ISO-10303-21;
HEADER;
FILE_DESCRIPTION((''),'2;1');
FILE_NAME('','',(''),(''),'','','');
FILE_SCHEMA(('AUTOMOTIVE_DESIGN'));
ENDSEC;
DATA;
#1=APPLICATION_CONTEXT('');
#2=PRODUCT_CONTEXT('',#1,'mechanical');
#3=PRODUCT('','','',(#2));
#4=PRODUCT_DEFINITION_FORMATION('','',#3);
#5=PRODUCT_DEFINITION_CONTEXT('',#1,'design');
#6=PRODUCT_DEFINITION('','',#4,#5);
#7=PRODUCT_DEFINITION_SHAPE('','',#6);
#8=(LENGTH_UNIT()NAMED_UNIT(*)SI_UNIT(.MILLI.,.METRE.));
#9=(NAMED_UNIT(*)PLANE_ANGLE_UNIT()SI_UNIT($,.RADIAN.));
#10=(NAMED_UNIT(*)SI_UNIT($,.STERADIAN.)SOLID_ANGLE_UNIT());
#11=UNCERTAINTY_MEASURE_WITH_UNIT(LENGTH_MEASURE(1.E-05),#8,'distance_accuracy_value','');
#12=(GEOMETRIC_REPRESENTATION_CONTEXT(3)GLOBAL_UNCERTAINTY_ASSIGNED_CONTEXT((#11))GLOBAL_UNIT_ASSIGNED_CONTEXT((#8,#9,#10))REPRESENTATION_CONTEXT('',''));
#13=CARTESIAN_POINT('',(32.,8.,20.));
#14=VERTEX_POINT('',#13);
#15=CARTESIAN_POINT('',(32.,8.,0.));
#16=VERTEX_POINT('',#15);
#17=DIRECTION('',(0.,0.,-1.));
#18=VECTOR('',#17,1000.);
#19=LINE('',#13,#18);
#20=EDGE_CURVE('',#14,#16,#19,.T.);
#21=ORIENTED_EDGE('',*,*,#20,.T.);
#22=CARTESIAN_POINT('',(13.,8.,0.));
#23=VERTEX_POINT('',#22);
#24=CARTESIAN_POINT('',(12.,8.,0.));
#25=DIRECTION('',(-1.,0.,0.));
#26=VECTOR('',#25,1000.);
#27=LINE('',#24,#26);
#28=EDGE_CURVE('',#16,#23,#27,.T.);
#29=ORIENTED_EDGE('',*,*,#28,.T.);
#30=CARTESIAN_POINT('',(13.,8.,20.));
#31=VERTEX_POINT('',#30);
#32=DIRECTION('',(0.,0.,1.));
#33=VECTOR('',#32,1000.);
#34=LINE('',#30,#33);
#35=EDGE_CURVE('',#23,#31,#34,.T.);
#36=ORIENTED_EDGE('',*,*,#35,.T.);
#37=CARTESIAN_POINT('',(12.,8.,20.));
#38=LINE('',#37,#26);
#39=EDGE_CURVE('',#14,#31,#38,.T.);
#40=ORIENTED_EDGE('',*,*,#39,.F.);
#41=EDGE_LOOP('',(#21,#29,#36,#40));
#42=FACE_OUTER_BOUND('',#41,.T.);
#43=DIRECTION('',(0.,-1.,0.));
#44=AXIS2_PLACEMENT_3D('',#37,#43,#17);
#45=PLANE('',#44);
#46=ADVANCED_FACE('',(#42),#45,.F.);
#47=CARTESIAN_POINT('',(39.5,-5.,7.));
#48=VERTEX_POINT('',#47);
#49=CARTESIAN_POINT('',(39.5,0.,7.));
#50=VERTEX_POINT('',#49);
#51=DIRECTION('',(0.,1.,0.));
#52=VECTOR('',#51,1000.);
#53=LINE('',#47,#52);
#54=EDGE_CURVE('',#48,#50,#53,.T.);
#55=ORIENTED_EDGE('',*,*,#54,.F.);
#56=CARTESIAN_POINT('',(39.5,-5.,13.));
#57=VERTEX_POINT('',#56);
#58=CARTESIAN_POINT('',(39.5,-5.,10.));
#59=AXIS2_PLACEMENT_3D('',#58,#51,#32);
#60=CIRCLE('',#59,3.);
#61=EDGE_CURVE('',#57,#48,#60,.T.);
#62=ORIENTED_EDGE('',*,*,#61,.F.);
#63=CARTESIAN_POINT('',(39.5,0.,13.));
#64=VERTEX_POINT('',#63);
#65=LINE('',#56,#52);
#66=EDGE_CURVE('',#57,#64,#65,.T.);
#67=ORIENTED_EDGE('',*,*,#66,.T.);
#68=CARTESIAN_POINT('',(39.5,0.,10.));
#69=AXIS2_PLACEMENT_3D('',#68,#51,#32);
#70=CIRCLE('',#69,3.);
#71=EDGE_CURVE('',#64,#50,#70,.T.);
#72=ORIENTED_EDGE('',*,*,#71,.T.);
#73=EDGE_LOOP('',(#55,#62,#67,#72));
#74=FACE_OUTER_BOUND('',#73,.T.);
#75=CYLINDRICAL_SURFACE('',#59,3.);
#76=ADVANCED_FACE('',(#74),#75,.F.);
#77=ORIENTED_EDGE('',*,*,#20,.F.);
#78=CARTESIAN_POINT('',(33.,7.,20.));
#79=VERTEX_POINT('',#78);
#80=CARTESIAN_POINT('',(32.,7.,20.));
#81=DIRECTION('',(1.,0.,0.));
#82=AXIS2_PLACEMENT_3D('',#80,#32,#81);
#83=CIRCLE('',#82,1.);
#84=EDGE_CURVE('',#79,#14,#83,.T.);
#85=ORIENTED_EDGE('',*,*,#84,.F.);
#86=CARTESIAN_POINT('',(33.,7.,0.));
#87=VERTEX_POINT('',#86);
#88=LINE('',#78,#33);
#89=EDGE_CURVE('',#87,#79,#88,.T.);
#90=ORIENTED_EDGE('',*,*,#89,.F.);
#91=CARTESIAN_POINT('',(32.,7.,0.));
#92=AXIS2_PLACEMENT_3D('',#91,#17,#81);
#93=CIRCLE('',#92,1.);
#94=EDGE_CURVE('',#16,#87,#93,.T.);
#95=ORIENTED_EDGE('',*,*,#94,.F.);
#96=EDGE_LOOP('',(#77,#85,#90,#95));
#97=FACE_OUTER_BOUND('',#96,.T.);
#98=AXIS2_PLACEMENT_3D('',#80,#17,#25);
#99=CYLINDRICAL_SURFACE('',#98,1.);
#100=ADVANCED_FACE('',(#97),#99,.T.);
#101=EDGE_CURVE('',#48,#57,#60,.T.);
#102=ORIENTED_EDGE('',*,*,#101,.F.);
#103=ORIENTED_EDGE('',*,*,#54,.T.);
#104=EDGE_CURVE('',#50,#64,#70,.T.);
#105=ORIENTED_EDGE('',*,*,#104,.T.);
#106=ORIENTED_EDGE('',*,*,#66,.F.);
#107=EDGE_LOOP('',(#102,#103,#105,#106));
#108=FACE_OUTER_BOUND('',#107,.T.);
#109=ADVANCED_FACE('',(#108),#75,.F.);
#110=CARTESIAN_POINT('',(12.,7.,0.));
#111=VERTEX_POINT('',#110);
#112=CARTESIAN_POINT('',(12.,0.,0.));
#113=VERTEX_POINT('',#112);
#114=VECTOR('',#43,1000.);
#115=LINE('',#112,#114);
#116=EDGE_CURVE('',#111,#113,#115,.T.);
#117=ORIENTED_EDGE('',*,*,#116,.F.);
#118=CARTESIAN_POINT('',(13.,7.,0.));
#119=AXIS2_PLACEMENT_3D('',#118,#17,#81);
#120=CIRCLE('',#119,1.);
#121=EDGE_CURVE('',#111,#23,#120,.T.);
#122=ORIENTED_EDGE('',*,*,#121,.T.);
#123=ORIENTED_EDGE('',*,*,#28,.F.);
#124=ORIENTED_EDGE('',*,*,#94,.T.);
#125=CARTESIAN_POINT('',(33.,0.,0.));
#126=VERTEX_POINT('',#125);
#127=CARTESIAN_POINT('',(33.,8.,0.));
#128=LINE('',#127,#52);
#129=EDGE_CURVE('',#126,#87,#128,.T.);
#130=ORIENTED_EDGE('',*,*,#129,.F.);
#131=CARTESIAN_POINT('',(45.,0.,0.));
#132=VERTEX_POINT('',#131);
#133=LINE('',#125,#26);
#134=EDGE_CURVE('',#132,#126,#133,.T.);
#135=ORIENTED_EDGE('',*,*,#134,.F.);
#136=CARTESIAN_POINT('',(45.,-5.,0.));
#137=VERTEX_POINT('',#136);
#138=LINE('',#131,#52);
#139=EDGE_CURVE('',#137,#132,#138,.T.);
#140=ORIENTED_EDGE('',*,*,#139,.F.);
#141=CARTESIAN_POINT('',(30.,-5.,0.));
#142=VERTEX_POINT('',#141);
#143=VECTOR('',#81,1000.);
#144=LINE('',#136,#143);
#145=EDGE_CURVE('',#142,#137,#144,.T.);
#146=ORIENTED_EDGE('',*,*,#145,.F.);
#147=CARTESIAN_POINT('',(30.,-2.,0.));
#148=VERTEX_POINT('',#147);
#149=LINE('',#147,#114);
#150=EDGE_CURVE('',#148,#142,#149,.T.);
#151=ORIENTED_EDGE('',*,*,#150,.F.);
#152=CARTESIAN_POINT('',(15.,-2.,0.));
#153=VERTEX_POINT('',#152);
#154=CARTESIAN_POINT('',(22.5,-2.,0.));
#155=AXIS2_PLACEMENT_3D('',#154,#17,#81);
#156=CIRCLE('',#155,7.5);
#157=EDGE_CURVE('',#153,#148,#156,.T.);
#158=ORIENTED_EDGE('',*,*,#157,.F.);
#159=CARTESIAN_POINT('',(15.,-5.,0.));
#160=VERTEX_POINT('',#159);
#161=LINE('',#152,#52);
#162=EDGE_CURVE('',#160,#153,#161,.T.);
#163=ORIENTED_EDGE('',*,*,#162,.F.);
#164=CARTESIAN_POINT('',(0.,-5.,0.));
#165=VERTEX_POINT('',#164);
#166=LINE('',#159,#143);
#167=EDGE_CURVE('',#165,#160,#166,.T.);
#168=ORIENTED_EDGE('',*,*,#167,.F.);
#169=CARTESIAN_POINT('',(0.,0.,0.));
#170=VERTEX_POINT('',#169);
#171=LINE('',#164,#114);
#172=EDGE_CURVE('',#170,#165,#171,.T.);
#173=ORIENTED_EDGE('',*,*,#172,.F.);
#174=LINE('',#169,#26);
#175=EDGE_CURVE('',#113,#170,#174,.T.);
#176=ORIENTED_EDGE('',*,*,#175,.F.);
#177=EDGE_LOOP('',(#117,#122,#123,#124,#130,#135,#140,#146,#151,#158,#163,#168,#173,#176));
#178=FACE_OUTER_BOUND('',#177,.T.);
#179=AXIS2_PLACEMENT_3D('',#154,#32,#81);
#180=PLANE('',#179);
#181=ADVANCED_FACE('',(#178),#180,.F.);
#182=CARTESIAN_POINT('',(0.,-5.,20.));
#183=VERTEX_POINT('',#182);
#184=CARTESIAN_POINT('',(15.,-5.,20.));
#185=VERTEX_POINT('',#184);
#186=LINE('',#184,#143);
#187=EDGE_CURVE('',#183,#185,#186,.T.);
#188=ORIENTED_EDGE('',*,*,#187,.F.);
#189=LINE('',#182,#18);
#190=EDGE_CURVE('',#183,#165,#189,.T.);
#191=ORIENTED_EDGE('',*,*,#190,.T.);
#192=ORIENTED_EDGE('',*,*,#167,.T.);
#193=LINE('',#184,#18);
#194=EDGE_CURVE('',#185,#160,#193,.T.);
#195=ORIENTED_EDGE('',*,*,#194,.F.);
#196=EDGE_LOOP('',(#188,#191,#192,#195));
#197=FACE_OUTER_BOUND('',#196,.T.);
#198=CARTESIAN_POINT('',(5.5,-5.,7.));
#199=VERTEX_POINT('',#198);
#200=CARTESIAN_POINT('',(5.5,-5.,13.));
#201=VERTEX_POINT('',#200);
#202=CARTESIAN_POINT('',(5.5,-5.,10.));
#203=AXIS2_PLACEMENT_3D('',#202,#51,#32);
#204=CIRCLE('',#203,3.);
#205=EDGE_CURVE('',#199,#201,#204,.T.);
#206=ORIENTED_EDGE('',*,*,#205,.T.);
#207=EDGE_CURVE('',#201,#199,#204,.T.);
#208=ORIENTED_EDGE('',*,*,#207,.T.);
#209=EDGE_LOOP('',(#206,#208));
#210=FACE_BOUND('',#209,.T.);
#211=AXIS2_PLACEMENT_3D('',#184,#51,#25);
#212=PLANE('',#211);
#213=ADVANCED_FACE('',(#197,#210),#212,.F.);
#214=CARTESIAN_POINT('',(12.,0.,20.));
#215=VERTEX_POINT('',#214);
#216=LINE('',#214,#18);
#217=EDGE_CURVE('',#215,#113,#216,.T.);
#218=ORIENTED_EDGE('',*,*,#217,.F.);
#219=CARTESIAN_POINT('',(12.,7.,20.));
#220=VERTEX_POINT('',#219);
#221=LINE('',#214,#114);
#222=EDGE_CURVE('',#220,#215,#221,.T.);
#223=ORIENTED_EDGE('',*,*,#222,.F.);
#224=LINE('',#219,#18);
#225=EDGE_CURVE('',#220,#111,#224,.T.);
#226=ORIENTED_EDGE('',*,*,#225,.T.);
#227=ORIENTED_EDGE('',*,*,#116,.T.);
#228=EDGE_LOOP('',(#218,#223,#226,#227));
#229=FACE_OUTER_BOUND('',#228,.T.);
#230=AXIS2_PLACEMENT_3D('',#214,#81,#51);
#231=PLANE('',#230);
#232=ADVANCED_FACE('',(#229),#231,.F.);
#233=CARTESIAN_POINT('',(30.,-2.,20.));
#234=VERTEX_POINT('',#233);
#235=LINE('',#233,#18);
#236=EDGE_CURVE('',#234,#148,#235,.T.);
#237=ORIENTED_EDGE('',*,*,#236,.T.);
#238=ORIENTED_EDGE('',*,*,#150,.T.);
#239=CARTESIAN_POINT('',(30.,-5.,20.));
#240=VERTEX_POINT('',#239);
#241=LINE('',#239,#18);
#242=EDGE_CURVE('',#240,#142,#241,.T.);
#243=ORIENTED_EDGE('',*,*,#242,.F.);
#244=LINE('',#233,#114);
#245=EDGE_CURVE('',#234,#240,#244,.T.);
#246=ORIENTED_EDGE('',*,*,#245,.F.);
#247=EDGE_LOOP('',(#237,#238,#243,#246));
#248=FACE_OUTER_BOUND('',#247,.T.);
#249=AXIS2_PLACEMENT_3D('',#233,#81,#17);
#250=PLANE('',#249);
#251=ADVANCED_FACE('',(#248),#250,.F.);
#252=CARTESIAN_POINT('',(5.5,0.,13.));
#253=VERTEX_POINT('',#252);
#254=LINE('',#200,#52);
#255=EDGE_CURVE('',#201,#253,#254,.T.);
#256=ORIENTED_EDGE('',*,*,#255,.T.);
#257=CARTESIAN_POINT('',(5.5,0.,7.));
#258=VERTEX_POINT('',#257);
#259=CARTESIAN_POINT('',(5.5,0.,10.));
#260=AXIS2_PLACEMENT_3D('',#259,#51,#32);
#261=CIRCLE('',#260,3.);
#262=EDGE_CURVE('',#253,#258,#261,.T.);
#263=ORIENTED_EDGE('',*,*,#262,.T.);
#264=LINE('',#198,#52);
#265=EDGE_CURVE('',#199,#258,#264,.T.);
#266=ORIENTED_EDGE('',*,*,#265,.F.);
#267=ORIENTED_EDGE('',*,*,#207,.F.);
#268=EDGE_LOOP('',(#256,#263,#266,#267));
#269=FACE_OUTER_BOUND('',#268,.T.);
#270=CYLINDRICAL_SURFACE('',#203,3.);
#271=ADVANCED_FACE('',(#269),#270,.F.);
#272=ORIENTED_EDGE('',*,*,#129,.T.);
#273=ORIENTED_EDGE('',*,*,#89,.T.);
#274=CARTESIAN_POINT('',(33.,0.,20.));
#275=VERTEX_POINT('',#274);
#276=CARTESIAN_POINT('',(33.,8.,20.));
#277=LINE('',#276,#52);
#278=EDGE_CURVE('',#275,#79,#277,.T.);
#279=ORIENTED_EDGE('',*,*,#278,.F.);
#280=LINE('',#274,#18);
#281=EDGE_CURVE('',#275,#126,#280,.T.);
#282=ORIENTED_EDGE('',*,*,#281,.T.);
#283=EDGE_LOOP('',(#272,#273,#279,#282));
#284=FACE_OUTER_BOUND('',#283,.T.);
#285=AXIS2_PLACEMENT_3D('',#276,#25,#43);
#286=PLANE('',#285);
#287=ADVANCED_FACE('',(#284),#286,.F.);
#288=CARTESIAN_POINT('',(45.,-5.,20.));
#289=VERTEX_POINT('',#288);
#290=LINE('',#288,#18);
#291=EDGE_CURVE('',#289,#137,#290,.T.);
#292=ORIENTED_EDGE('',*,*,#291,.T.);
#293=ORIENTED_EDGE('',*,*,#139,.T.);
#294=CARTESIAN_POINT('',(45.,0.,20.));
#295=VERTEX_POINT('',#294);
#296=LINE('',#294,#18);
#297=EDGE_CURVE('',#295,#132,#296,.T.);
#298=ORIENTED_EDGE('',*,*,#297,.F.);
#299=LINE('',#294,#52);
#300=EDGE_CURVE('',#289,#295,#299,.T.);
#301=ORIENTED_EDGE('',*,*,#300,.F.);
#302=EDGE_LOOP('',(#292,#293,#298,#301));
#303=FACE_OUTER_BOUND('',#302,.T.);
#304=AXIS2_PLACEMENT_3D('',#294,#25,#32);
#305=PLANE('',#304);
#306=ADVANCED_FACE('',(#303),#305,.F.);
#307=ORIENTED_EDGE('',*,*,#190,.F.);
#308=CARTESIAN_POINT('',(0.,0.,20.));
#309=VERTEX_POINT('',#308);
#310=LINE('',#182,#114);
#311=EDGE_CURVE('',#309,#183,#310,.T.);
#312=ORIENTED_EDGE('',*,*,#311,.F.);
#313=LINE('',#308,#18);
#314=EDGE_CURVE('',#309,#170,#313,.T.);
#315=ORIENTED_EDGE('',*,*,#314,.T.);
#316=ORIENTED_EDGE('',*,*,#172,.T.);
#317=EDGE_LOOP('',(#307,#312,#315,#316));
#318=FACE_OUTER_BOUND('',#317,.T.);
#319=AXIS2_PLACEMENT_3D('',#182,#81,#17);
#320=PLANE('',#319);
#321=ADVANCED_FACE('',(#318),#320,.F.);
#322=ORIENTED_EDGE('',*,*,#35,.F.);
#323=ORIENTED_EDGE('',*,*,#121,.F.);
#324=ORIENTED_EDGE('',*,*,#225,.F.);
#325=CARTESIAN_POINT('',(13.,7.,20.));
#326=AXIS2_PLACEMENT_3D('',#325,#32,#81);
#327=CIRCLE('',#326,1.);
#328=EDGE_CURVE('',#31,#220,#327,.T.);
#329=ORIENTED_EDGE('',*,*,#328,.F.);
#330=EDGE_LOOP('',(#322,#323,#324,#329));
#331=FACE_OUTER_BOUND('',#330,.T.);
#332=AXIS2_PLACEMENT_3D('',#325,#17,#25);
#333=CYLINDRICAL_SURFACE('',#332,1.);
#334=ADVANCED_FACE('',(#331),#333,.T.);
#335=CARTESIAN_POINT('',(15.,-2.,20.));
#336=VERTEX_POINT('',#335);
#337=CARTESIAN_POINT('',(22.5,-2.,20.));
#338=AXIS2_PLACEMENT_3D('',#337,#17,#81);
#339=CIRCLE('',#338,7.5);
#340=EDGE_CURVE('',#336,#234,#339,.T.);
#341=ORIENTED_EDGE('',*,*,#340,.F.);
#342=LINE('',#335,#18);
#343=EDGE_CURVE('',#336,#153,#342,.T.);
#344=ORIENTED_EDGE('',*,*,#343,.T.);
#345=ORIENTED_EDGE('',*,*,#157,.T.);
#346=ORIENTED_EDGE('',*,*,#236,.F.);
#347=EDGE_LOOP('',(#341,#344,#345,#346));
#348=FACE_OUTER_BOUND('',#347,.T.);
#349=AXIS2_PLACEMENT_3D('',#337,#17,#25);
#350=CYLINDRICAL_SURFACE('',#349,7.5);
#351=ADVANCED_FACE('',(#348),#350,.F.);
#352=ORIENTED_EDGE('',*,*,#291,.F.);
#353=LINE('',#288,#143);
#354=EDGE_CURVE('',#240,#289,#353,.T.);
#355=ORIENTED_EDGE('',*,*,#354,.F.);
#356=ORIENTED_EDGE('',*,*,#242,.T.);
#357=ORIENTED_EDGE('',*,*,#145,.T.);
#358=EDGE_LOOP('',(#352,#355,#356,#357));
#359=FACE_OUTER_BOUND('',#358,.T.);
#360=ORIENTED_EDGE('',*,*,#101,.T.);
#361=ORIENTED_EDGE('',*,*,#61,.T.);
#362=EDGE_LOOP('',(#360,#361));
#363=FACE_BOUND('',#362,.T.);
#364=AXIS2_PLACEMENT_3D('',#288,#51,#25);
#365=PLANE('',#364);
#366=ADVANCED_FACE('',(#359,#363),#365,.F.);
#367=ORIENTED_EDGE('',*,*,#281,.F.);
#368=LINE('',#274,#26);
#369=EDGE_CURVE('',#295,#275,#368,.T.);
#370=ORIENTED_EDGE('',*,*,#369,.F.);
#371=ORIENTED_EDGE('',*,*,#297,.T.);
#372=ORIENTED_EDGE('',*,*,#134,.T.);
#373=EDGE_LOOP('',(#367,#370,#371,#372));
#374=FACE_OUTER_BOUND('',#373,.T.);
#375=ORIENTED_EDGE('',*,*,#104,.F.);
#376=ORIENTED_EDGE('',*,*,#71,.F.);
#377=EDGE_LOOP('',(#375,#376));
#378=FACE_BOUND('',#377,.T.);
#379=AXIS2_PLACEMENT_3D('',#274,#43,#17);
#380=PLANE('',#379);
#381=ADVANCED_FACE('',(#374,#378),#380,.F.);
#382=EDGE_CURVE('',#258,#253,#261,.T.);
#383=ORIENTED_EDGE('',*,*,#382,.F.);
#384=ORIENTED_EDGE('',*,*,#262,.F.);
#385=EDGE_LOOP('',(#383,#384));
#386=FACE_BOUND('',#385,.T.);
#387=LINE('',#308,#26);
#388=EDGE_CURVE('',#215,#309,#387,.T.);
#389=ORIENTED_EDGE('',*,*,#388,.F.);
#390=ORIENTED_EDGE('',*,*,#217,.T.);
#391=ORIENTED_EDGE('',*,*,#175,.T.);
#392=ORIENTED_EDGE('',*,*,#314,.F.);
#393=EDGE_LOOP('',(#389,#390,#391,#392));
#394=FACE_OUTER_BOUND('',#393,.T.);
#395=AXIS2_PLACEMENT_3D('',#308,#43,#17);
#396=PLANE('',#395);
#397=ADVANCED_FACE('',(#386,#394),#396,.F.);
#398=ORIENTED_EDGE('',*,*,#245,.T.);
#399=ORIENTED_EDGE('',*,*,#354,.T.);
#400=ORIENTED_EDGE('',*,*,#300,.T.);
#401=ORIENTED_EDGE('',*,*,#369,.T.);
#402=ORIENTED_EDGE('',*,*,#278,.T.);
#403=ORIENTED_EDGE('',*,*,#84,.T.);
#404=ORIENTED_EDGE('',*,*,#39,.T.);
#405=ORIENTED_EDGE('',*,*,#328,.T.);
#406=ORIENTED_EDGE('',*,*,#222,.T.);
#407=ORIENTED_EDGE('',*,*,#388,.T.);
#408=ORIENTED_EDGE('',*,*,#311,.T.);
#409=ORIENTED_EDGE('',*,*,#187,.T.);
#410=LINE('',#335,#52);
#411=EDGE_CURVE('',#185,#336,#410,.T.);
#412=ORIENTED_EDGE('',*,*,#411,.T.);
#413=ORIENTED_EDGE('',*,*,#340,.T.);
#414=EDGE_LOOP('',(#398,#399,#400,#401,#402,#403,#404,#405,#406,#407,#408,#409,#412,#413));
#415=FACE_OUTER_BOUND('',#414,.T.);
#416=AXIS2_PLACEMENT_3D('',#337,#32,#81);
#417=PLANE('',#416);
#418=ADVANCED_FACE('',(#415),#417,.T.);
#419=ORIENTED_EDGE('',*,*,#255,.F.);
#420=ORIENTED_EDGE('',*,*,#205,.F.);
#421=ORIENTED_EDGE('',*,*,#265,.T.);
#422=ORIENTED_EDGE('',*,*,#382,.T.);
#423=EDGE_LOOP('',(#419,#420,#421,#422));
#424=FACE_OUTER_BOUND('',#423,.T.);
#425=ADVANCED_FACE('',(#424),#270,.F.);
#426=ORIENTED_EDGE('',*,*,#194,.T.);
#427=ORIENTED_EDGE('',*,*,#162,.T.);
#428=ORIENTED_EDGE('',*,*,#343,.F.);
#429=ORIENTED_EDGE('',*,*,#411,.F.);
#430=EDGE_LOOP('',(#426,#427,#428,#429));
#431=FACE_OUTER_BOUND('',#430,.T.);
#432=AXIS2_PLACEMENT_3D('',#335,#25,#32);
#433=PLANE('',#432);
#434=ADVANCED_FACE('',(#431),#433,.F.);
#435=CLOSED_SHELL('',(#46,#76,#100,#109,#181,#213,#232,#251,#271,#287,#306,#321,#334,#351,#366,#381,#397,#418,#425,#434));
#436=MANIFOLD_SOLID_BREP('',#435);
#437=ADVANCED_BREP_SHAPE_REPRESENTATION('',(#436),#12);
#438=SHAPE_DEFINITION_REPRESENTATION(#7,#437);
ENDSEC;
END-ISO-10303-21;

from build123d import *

# Parameters (mm, degrees)
EXTRUDE_1_DEPTH     = 20
FILLET_1_R          = 1
SKETCH_2_R          = 3
CUT_EXTRUDE_1_DEPTH = 50.889878733


with BuildPart() as part:
    # 草图1 → 凸台-拉伸1 (new body)
    with BuildSketch(Plane.XY):
        with BuildLine():
            Line((0, 0), (12, 0))
            Line((12, 0), (12, 8))
            Line((12, 8), (33, 8))
            Line((33, 8), (33, 0))
            Line((33, 0), (45, 0))
            Line((45, 0), (45, -5))
            Line((45, -5), (30, -5))
            Line((30, -5), (30, -2))
            ThreePointArc((30, -2), (22.5, 5.5), (15, -2))
            Line((15, -2), (15, -5))
            Line((15, -5), (0, -5))
            Line((0, -5), (0, 0))
        make_face()
    extrude(amount=EXTRUDE_1_DEPTH)

    # 圆角1
    fillet_1_edges = [part.edges().sort_by_distance(p)[0] for p in [
        (12, 8, 10),
        (33, 8, 10),
    ]]
    fillet(fillet_1_edges, radius=FILLET_1_R)

    # 草图2 → 切除-拉伸1 (cut, through all)
    with BuildSketch(Plane(origin=(0, 0, 0), x_dir=(1, 0, 0), z_dir=(0, 1, 0))):
        with Locations(Location((5.5, -10, 0), (0, 0, 270))):
            Circle(SKETCH_2_R)
        with Locations(Location((39.5, -10, 0), (0, 0, 270))):
            Circle(SKETCH_2_R)
    extrude(amount=-CUT_EXTRUDE_1_DEPTH, mode=Mode.SUBTRACT)


solid = part.part
